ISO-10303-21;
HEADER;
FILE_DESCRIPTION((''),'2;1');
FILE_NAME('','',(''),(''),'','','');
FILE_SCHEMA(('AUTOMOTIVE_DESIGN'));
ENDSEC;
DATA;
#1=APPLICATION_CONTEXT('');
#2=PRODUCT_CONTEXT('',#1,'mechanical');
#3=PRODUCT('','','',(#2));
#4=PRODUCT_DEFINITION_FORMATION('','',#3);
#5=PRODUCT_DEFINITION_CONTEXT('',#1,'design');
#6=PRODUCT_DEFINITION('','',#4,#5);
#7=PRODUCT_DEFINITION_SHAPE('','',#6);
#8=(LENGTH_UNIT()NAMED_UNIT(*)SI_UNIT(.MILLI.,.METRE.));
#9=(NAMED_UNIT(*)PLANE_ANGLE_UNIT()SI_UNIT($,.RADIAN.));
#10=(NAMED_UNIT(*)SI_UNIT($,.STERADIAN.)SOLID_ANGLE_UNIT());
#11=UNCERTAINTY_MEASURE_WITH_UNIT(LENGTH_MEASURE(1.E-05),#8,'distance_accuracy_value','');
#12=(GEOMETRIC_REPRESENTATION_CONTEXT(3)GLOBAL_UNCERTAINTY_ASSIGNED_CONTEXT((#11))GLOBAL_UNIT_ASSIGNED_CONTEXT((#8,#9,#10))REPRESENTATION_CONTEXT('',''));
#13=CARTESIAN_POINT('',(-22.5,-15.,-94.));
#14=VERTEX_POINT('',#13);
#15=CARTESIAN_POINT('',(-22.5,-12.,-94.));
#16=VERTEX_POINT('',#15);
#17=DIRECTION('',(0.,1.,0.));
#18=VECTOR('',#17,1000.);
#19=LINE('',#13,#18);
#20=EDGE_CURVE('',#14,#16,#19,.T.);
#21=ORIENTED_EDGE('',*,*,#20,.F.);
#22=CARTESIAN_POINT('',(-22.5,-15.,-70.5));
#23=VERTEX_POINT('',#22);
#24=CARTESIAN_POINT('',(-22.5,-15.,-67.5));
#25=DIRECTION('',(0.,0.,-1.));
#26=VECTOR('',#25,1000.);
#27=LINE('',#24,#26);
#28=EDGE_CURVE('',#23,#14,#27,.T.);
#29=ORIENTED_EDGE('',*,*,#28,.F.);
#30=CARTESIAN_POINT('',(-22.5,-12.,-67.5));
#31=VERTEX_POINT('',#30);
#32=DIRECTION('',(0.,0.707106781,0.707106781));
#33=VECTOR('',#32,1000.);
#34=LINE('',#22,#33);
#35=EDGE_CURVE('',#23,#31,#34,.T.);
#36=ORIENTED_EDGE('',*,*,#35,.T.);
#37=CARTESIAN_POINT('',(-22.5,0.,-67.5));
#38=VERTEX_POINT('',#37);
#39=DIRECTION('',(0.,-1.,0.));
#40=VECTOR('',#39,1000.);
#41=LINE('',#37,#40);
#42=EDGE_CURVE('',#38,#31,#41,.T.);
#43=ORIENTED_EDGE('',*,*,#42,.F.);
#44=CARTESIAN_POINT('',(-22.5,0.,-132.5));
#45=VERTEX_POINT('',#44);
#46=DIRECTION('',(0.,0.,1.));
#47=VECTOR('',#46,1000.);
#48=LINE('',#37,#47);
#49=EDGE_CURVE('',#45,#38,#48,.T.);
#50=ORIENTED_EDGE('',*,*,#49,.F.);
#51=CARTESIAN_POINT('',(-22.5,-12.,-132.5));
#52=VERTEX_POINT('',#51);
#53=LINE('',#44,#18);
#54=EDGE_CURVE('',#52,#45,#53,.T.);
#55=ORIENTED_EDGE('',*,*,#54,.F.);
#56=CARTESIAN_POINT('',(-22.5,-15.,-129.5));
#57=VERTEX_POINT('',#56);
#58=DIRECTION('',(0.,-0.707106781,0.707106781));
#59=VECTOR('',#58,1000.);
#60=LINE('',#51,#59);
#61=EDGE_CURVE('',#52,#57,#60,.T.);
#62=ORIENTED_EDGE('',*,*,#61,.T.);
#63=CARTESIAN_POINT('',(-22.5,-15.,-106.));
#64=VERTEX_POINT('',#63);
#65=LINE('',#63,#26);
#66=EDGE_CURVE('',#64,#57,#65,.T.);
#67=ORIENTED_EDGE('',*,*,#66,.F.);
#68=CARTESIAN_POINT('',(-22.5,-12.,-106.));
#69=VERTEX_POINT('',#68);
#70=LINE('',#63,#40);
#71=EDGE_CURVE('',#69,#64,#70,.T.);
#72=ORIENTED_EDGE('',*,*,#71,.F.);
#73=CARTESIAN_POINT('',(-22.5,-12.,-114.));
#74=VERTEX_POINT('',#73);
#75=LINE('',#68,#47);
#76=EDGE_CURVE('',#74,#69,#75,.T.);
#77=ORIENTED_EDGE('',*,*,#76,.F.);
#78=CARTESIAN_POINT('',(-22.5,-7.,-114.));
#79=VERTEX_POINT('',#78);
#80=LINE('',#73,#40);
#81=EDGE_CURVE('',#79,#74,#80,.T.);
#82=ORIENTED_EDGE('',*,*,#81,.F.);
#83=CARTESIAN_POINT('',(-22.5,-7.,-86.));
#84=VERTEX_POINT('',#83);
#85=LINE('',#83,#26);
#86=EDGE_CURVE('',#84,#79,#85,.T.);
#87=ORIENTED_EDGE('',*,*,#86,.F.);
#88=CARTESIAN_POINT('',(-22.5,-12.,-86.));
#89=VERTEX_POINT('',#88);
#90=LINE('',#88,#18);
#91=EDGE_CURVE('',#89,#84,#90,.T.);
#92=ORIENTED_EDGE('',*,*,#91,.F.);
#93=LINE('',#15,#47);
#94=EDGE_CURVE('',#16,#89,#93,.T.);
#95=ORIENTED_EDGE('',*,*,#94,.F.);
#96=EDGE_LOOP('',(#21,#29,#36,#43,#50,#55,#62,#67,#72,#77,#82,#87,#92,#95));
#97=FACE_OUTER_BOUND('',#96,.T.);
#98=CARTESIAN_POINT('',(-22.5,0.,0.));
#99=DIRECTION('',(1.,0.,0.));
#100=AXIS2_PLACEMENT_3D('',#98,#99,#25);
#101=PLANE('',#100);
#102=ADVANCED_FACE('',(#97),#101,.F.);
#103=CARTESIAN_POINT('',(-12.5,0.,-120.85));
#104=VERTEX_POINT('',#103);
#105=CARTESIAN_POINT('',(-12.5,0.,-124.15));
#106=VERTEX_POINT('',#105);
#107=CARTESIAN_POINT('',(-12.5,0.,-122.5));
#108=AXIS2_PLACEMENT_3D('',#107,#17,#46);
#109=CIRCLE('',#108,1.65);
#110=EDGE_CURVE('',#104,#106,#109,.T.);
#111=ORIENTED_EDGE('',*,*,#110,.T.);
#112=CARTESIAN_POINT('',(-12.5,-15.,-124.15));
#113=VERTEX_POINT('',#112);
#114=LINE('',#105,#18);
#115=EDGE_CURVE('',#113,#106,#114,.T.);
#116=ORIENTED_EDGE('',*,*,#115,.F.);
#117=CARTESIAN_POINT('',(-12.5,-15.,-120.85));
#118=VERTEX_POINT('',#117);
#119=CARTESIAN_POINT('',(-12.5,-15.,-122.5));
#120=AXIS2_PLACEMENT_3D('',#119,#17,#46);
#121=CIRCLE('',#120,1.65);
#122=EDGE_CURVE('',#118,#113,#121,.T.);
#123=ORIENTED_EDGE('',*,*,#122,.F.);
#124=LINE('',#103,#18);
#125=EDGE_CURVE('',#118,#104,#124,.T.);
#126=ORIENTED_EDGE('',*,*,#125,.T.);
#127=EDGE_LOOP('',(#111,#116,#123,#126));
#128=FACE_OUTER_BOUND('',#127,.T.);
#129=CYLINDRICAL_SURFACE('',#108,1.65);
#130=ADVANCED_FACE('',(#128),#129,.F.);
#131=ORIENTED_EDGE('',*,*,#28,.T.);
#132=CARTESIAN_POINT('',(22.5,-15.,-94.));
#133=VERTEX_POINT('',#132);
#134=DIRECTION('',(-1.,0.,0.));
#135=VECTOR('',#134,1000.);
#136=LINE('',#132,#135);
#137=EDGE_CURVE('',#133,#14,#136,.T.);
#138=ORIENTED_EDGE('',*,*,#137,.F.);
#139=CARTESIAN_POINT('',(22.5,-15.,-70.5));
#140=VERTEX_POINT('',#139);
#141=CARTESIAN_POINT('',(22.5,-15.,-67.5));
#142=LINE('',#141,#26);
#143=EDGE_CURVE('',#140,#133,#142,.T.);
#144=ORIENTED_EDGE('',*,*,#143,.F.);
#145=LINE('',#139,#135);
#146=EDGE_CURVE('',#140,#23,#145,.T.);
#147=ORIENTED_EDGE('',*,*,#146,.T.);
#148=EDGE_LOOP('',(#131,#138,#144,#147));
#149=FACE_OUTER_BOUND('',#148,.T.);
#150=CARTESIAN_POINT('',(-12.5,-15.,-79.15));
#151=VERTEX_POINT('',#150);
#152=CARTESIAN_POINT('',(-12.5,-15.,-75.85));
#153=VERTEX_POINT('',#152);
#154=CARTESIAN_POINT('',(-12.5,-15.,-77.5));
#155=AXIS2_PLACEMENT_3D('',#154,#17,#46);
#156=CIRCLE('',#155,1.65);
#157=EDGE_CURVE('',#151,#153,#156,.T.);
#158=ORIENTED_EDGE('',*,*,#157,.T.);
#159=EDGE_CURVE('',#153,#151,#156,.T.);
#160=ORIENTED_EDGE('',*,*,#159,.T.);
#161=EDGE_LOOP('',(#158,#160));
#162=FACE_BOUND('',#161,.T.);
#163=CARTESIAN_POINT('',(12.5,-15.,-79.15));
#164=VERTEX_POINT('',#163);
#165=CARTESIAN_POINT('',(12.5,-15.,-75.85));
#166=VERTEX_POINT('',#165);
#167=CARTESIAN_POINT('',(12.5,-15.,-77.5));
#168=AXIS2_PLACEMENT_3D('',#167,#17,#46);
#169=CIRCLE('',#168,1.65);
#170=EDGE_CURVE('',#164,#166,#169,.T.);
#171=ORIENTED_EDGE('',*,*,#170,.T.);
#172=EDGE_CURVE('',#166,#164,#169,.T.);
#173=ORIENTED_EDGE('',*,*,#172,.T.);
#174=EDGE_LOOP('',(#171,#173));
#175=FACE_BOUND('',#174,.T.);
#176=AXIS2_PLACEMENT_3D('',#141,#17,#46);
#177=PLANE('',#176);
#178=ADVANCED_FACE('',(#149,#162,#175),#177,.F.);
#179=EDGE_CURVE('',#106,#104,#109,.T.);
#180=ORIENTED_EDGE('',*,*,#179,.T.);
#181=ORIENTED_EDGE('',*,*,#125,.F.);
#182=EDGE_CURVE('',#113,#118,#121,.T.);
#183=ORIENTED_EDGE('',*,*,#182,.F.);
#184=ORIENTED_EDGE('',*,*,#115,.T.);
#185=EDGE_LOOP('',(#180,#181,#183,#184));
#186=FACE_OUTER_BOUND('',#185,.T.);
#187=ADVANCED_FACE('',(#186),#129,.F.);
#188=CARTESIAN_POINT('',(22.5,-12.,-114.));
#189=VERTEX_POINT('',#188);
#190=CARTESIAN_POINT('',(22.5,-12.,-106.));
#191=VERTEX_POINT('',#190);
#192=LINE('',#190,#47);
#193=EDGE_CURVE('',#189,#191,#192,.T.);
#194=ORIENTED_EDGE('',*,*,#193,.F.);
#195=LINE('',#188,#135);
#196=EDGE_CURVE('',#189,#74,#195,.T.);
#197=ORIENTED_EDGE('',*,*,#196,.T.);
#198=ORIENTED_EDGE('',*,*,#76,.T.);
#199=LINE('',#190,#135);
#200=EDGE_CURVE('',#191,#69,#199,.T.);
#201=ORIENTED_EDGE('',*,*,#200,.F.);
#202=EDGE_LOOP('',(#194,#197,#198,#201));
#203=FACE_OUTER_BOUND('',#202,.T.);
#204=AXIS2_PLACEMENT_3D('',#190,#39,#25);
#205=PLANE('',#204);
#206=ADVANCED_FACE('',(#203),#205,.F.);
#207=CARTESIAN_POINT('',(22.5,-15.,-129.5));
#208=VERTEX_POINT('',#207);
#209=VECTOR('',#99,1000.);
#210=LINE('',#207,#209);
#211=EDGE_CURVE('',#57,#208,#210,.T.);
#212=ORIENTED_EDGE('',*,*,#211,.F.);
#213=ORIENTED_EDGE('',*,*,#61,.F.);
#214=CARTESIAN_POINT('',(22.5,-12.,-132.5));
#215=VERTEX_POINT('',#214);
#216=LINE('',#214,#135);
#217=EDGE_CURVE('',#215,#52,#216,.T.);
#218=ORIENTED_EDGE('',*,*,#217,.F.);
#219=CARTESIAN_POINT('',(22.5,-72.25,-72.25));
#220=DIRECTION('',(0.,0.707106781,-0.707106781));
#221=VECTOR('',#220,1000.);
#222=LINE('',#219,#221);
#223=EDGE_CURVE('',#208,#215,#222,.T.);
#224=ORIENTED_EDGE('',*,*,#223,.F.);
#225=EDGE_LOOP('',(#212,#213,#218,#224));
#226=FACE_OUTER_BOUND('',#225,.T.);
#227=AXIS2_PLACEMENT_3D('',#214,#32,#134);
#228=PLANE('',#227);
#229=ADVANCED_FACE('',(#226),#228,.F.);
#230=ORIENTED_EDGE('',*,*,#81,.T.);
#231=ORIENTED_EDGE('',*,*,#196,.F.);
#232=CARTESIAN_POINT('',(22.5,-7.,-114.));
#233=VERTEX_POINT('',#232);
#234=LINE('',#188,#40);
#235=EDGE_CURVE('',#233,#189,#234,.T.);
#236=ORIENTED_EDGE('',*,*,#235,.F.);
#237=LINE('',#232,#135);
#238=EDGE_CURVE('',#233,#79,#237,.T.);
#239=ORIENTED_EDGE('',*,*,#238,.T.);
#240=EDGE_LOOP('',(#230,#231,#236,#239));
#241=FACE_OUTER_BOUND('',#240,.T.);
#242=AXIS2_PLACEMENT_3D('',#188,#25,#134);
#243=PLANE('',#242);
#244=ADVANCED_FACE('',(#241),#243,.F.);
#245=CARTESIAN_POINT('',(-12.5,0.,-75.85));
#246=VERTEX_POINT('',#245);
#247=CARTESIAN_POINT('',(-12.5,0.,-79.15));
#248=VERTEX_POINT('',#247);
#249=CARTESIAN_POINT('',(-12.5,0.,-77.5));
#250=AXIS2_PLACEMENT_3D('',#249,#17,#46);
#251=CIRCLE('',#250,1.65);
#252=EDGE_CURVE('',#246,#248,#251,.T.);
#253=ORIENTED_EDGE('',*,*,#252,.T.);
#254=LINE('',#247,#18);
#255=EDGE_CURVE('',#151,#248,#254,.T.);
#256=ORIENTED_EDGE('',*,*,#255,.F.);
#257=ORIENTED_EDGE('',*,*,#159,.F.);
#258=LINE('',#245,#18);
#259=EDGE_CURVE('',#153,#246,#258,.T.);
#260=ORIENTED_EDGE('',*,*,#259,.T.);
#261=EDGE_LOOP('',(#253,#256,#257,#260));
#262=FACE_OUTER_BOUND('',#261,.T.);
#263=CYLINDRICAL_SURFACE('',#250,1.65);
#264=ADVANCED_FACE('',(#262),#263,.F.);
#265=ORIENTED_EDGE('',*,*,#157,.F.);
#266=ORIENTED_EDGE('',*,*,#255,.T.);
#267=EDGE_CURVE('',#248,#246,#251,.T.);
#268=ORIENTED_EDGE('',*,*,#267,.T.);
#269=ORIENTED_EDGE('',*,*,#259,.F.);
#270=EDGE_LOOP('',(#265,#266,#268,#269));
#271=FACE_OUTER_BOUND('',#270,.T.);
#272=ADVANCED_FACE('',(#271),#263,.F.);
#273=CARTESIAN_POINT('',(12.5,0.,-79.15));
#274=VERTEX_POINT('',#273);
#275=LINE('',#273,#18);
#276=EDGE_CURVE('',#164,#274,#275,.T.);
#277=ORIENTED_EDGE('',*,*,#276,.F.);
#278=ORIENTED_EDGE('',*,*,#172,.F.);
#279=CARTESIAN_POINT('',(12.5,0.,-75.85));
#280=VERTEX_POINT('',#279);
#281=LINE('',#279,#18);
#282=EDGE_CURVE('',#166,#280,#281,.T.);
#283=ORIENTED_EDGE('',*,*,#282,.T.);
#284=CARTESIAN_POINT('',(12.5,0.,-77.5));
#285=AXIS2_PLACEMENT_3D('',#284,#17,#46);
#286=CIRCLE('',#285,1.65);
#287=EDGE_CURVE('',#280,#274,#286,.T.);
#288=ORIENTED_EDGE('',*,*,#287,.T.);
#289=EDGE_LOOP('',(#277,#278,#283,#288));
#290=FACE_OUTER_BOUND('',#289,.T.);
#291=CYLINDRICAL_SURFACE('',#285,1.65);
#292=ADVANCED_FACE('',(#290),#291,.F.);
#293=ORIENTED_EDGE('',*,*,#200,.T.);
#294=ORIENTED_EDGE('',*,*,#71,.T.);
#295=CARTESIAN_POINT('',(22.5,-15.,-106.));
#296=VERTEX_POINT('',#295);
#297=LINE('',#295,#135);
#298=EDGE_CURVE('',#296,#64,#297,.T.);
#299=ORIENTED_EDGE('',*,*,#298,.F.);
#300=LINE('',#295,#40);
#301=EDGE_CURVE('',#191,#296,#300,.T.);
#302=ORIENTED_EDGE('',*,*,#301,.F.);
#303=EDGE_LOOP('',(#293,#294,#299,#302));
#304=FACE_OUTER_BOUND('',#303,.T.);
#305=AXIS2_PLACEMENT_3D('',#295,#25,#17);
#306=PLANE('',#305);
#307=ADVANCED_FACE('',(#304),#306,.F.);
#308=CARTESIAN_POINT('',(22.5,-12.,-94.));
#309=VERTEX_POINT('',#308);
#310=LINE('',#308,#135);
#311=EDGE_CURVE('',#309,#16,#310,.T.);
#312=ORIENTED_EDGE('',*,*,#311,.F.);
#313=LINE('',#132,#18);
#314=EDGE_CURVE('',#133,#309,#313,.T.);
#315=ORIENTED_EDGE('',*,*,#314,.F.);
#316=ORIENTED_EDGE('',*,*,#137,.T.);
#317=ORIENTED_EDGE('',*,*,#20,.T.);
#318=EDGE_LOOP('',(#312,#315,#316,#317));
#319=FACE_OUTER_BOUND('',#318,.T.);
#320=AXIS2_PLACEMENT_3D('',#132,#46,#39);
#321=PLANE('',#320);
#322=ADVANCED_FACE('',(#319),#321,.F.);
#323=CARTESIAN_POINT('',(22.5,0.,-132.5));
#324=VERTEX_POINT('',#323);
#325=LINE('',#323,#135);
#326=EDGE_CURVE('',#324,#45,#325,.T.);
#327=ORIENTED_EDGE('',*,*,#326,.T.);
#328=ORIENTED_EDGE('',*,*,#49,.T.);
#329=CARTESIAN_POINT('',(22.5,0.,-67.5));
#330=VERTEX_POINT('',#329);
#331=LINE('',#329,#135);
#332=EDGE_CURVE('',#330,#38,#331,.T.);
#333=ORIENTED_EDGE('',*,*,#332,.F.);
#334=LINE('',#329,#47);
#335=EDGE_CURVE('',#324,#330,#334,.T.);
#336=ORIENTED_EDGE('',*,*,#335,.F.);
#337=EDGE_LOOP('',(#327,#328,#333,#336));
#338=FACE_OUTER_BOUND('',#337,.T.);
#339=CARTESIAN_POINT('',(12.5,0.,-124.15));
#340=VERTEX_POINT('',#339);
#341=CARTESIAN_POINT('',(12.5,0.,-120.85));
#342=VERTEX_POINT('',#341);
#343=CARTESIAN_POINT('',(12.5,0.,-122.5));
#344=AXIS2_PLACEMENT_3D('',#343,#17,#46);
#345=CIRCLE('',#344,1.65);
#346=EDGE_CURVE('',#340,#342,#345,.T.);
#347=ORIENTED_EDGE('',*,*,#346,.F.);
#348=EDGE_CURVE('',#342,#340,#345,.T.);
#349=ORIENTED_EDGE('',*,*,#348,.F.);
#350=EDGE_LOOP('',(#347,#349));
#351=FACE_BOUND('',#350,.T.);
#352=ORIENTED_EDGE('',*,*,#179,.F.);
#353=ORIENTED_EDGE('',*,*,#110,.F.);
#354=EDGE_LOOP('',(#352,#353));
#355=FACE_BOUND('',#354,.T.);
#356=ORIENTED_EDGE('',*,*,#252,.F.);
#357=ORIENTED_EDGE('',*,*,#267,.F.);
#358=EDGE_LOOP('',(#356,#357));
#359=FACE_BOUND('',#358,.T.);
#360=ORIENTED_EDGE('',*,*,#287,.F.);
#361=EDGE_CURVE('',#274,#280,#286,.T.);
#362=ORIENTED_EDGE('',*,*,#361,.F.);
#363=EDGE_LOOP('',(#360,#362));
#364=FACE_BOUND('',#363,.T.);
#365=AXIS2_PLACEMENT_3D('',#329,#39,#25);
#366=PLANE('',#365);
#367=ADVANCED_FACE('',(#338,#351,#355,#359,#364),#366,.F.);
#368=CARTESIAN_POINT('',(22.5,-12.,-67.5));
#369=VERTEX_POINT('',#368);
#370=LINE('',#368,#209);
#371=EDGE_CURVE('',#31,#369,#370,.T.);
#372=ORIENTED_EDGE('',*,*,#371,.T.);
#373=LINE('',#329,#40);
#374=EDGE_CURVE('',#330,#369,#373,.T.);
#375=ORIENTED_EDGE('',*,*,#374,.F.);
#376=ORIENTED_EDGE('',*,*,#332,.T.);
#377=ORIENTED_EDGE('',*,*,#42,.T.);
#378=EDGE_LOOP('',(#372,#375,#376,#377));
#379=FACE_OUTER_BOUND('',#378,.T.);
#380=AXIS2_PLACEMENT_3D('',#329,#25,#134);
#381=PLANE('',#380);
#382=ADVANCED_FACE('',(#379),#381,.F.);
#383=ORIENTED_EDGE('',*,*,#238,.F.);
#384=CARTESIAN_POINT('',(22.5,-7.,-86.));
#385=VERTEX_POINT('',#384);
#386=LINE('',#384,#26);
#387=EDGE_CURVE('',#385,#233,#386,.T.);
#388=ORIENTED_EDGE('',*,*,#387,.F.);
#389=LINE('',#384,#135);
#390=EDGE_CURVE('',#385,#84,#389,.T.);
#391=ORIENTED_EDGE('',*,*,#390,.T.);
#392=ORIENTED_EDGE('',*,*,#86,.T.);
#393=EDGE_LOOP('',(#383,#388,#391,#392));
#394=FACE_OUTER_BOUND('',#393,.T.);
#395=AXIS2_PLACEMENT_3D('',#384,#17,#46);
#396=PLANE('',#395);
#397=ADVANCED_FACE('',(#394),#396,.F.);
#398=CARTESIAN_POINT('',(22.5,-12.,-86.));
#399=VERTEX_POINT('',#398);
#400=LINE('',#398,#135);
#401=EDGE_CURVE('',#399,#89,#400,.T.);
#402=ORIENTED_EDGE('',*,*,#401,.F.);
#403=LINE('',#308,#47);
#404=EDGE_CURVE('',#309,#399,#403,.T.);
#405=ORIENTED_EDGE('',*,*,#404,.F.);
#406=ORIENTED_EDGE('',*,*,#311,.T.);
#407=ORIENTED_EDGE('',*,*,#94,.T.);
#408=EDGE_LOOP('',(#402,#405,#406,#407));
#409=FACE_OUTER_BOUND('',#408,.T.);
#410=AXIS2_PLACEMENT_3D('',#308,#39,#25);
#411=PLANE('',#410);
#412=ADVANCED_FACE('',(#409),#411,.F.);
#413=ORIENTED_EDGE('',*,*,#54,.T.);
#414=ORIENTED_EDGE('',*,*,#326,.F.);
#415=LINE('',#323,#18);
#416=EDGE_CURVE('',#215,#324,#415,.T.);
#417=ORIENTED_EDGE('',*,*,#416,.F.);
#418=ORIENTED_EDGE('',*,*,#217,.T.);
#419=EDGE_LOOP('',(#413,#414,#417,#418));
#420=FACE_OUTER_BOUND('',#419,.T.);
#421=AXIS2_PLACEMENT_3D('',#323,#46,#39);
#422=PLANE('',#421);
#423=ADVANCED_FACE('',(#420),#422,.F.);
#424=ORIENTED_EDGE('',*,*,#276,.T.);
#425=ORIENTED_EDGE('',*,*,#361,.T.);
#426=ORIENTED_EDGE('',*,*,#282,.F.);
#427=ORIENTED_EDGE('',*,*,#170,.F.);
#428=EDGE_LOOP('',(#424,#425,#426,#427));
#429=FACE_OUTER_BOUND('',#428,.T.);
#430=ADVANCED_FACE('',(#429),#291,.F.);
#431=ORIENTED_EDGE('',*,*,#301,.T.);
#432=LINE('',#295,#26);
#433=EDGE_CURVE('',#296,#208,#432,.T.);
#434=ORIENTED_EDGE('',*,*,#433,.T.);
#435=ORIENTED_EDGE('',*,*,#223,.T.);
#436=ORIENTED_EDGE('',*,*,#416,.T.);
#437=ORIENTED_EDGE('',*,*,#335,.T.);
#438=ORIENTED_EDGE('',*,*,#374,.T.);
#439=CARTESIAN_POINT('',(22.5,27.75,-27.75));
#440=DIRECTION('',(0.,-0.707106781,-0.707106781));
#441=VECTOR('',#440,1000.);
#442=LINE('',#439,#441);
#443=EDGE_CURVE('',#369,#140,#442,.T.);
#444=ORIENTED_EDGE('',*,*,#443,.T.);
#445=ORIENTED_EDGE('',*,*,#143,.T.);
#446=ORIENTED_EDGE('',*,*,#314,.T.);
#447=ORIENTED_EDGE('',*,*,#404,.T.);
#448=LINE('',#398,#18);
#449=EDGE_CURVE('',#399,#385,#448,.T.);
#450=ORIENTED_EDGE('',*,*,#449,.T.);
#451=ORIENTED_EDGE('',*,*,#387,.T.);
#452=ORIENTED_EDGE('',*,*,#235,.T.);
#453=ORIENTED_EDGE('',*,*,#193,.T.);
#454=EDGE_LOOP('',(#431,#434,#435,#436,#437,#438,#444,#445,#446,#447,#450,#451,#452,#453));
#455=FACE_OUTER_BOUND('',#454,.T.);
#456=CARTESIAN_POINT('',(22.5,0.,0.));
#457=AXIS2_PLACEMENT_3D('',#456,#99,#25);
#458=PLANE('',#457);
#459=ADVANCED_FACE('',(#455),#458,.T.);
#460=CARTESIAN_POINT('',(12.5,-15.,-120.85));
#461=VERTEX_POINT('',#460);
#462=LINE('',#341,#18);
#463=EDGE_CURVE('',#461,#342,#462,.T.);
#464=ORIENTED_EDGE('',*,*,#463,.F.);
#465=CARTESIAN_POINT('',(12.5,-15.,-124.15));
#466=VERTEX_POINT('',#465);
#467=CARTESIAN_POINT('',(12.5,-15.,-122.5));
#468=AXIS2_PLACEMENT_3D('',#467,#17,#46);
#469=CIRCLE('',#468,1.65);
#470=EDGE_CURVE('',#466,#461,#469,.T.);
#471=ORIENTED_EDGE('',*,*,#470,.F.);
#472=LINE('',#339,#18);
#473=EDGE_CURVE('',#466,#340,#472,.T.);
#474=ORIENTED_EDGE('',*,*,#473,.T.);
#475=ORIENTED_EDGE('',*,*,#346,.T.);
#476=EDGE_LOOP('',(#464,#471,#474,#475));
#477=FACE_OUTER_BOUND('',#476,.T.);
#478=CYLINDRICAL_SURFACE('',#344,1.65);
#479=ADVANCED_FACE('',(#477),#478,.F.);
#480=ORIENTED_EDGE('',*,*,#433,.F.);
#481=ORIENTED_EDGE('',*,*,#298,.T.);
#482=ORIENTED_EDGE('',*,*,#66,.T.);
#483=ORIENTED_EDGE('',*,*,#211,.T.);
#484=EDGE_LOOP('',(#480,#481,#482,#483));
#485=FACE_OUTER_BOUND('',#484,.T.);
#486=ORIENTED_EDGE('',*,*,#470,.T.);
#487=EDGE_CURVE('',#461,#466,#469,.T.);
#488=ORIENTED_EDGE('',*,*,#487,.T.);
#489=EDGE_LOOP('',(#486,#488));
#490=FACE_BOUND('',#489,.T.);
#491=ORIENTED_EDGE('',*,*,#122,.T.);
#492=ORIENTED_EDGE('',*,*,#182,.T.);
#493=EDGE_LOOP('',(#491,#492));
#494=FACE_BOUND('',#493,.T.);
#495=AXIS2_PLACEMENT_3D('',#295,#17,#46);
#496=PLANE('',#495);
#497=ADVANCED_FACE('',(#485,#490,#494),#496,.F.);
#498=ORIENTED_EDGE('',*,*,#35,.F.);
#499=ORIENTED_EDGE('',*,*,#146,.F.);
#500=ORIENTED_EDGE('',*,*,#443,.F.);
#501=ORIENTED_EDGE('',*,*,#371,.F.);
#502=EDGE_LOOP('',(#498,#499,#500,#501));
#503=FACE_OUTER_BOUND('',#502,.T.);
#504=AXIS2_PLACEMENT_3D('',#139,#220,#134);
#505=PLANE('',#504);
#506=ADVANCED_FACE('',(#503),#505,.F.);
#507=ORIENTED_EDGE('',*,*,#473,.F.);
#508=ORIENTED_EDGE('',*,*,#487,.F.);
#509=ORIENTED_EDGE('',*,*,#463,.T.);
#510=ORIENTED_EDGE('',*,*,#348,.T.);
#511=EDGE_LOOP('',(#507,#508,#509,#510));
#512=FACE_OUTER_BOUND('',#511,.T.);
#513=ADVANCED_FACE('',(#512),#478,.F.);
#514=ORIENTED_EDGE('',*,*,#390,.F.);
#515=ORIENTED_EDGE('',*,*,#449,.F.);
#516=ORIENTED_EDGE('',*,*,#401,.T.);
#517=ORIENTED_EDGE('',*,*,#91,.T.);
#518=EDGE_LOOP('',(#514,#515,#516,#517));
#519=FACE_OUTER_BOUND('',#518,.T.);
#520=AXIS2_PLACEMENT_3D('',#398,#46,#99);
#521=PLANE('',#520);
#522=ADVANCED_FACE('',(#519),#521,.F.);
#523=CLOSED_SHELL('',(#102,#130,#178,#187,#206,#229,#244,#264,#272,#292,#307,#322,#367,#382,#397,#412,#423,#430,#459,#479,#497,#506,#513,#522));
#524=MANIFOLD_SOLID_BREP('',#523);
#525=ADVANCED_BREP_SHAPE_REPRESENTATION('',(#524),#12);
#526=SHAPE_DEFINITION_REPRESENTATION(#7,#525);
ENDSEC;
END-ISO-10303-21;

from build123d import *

# Parameters (mm, degrees)
BOSS_EXTRUDE1_DEPTH = 22.5
CHAMFER1_SIZE       = 3
M4_TAPPED_HOLE1_D   = 3.3


with BuildPart() as part:
    # Sketch2 → Boss-Extrude1 (new, symmetric)
    with BuildSketch(Plane(origin=(0, 0, 0), x_dir=(0, 0, -1), z_dir=(1, 0, 0))):
        Polygon((67.5, 0), (132.5, 0), (132.5, -15), (106, -15), (106, -12), (114, -12), (114, -7), (86, -7), (86, -12), (94, -12), (94, -15), (67.5, -15), align=None)
    extrude(amount=BOSS_EXTRUDE1_DEPTH, both=True)

    # Chamfer1
    chamfer1_edges = [part.edges().sort_by_distance(p)[0] for p in [
        (0, -15, -132.5),
        (0, -15, -67.5),
    ]]
    chamfer(chamfer1_edges, length=CHAMFER1_SIZE)

    # M4 Tapped Hole1 (through all)
    with Locations(Plane(origin=(0, 0, 0), x_dir=(1, 0, 0), z_dir=(0, 1, 0))):
        with Locations((-12.5, 122.5), (12.5, 122.5), (-12.5, 77.5), (12.5, 77.5)):
            Hole(M4_TAPPED_HOLE1_D / 2)


solid = part.part
